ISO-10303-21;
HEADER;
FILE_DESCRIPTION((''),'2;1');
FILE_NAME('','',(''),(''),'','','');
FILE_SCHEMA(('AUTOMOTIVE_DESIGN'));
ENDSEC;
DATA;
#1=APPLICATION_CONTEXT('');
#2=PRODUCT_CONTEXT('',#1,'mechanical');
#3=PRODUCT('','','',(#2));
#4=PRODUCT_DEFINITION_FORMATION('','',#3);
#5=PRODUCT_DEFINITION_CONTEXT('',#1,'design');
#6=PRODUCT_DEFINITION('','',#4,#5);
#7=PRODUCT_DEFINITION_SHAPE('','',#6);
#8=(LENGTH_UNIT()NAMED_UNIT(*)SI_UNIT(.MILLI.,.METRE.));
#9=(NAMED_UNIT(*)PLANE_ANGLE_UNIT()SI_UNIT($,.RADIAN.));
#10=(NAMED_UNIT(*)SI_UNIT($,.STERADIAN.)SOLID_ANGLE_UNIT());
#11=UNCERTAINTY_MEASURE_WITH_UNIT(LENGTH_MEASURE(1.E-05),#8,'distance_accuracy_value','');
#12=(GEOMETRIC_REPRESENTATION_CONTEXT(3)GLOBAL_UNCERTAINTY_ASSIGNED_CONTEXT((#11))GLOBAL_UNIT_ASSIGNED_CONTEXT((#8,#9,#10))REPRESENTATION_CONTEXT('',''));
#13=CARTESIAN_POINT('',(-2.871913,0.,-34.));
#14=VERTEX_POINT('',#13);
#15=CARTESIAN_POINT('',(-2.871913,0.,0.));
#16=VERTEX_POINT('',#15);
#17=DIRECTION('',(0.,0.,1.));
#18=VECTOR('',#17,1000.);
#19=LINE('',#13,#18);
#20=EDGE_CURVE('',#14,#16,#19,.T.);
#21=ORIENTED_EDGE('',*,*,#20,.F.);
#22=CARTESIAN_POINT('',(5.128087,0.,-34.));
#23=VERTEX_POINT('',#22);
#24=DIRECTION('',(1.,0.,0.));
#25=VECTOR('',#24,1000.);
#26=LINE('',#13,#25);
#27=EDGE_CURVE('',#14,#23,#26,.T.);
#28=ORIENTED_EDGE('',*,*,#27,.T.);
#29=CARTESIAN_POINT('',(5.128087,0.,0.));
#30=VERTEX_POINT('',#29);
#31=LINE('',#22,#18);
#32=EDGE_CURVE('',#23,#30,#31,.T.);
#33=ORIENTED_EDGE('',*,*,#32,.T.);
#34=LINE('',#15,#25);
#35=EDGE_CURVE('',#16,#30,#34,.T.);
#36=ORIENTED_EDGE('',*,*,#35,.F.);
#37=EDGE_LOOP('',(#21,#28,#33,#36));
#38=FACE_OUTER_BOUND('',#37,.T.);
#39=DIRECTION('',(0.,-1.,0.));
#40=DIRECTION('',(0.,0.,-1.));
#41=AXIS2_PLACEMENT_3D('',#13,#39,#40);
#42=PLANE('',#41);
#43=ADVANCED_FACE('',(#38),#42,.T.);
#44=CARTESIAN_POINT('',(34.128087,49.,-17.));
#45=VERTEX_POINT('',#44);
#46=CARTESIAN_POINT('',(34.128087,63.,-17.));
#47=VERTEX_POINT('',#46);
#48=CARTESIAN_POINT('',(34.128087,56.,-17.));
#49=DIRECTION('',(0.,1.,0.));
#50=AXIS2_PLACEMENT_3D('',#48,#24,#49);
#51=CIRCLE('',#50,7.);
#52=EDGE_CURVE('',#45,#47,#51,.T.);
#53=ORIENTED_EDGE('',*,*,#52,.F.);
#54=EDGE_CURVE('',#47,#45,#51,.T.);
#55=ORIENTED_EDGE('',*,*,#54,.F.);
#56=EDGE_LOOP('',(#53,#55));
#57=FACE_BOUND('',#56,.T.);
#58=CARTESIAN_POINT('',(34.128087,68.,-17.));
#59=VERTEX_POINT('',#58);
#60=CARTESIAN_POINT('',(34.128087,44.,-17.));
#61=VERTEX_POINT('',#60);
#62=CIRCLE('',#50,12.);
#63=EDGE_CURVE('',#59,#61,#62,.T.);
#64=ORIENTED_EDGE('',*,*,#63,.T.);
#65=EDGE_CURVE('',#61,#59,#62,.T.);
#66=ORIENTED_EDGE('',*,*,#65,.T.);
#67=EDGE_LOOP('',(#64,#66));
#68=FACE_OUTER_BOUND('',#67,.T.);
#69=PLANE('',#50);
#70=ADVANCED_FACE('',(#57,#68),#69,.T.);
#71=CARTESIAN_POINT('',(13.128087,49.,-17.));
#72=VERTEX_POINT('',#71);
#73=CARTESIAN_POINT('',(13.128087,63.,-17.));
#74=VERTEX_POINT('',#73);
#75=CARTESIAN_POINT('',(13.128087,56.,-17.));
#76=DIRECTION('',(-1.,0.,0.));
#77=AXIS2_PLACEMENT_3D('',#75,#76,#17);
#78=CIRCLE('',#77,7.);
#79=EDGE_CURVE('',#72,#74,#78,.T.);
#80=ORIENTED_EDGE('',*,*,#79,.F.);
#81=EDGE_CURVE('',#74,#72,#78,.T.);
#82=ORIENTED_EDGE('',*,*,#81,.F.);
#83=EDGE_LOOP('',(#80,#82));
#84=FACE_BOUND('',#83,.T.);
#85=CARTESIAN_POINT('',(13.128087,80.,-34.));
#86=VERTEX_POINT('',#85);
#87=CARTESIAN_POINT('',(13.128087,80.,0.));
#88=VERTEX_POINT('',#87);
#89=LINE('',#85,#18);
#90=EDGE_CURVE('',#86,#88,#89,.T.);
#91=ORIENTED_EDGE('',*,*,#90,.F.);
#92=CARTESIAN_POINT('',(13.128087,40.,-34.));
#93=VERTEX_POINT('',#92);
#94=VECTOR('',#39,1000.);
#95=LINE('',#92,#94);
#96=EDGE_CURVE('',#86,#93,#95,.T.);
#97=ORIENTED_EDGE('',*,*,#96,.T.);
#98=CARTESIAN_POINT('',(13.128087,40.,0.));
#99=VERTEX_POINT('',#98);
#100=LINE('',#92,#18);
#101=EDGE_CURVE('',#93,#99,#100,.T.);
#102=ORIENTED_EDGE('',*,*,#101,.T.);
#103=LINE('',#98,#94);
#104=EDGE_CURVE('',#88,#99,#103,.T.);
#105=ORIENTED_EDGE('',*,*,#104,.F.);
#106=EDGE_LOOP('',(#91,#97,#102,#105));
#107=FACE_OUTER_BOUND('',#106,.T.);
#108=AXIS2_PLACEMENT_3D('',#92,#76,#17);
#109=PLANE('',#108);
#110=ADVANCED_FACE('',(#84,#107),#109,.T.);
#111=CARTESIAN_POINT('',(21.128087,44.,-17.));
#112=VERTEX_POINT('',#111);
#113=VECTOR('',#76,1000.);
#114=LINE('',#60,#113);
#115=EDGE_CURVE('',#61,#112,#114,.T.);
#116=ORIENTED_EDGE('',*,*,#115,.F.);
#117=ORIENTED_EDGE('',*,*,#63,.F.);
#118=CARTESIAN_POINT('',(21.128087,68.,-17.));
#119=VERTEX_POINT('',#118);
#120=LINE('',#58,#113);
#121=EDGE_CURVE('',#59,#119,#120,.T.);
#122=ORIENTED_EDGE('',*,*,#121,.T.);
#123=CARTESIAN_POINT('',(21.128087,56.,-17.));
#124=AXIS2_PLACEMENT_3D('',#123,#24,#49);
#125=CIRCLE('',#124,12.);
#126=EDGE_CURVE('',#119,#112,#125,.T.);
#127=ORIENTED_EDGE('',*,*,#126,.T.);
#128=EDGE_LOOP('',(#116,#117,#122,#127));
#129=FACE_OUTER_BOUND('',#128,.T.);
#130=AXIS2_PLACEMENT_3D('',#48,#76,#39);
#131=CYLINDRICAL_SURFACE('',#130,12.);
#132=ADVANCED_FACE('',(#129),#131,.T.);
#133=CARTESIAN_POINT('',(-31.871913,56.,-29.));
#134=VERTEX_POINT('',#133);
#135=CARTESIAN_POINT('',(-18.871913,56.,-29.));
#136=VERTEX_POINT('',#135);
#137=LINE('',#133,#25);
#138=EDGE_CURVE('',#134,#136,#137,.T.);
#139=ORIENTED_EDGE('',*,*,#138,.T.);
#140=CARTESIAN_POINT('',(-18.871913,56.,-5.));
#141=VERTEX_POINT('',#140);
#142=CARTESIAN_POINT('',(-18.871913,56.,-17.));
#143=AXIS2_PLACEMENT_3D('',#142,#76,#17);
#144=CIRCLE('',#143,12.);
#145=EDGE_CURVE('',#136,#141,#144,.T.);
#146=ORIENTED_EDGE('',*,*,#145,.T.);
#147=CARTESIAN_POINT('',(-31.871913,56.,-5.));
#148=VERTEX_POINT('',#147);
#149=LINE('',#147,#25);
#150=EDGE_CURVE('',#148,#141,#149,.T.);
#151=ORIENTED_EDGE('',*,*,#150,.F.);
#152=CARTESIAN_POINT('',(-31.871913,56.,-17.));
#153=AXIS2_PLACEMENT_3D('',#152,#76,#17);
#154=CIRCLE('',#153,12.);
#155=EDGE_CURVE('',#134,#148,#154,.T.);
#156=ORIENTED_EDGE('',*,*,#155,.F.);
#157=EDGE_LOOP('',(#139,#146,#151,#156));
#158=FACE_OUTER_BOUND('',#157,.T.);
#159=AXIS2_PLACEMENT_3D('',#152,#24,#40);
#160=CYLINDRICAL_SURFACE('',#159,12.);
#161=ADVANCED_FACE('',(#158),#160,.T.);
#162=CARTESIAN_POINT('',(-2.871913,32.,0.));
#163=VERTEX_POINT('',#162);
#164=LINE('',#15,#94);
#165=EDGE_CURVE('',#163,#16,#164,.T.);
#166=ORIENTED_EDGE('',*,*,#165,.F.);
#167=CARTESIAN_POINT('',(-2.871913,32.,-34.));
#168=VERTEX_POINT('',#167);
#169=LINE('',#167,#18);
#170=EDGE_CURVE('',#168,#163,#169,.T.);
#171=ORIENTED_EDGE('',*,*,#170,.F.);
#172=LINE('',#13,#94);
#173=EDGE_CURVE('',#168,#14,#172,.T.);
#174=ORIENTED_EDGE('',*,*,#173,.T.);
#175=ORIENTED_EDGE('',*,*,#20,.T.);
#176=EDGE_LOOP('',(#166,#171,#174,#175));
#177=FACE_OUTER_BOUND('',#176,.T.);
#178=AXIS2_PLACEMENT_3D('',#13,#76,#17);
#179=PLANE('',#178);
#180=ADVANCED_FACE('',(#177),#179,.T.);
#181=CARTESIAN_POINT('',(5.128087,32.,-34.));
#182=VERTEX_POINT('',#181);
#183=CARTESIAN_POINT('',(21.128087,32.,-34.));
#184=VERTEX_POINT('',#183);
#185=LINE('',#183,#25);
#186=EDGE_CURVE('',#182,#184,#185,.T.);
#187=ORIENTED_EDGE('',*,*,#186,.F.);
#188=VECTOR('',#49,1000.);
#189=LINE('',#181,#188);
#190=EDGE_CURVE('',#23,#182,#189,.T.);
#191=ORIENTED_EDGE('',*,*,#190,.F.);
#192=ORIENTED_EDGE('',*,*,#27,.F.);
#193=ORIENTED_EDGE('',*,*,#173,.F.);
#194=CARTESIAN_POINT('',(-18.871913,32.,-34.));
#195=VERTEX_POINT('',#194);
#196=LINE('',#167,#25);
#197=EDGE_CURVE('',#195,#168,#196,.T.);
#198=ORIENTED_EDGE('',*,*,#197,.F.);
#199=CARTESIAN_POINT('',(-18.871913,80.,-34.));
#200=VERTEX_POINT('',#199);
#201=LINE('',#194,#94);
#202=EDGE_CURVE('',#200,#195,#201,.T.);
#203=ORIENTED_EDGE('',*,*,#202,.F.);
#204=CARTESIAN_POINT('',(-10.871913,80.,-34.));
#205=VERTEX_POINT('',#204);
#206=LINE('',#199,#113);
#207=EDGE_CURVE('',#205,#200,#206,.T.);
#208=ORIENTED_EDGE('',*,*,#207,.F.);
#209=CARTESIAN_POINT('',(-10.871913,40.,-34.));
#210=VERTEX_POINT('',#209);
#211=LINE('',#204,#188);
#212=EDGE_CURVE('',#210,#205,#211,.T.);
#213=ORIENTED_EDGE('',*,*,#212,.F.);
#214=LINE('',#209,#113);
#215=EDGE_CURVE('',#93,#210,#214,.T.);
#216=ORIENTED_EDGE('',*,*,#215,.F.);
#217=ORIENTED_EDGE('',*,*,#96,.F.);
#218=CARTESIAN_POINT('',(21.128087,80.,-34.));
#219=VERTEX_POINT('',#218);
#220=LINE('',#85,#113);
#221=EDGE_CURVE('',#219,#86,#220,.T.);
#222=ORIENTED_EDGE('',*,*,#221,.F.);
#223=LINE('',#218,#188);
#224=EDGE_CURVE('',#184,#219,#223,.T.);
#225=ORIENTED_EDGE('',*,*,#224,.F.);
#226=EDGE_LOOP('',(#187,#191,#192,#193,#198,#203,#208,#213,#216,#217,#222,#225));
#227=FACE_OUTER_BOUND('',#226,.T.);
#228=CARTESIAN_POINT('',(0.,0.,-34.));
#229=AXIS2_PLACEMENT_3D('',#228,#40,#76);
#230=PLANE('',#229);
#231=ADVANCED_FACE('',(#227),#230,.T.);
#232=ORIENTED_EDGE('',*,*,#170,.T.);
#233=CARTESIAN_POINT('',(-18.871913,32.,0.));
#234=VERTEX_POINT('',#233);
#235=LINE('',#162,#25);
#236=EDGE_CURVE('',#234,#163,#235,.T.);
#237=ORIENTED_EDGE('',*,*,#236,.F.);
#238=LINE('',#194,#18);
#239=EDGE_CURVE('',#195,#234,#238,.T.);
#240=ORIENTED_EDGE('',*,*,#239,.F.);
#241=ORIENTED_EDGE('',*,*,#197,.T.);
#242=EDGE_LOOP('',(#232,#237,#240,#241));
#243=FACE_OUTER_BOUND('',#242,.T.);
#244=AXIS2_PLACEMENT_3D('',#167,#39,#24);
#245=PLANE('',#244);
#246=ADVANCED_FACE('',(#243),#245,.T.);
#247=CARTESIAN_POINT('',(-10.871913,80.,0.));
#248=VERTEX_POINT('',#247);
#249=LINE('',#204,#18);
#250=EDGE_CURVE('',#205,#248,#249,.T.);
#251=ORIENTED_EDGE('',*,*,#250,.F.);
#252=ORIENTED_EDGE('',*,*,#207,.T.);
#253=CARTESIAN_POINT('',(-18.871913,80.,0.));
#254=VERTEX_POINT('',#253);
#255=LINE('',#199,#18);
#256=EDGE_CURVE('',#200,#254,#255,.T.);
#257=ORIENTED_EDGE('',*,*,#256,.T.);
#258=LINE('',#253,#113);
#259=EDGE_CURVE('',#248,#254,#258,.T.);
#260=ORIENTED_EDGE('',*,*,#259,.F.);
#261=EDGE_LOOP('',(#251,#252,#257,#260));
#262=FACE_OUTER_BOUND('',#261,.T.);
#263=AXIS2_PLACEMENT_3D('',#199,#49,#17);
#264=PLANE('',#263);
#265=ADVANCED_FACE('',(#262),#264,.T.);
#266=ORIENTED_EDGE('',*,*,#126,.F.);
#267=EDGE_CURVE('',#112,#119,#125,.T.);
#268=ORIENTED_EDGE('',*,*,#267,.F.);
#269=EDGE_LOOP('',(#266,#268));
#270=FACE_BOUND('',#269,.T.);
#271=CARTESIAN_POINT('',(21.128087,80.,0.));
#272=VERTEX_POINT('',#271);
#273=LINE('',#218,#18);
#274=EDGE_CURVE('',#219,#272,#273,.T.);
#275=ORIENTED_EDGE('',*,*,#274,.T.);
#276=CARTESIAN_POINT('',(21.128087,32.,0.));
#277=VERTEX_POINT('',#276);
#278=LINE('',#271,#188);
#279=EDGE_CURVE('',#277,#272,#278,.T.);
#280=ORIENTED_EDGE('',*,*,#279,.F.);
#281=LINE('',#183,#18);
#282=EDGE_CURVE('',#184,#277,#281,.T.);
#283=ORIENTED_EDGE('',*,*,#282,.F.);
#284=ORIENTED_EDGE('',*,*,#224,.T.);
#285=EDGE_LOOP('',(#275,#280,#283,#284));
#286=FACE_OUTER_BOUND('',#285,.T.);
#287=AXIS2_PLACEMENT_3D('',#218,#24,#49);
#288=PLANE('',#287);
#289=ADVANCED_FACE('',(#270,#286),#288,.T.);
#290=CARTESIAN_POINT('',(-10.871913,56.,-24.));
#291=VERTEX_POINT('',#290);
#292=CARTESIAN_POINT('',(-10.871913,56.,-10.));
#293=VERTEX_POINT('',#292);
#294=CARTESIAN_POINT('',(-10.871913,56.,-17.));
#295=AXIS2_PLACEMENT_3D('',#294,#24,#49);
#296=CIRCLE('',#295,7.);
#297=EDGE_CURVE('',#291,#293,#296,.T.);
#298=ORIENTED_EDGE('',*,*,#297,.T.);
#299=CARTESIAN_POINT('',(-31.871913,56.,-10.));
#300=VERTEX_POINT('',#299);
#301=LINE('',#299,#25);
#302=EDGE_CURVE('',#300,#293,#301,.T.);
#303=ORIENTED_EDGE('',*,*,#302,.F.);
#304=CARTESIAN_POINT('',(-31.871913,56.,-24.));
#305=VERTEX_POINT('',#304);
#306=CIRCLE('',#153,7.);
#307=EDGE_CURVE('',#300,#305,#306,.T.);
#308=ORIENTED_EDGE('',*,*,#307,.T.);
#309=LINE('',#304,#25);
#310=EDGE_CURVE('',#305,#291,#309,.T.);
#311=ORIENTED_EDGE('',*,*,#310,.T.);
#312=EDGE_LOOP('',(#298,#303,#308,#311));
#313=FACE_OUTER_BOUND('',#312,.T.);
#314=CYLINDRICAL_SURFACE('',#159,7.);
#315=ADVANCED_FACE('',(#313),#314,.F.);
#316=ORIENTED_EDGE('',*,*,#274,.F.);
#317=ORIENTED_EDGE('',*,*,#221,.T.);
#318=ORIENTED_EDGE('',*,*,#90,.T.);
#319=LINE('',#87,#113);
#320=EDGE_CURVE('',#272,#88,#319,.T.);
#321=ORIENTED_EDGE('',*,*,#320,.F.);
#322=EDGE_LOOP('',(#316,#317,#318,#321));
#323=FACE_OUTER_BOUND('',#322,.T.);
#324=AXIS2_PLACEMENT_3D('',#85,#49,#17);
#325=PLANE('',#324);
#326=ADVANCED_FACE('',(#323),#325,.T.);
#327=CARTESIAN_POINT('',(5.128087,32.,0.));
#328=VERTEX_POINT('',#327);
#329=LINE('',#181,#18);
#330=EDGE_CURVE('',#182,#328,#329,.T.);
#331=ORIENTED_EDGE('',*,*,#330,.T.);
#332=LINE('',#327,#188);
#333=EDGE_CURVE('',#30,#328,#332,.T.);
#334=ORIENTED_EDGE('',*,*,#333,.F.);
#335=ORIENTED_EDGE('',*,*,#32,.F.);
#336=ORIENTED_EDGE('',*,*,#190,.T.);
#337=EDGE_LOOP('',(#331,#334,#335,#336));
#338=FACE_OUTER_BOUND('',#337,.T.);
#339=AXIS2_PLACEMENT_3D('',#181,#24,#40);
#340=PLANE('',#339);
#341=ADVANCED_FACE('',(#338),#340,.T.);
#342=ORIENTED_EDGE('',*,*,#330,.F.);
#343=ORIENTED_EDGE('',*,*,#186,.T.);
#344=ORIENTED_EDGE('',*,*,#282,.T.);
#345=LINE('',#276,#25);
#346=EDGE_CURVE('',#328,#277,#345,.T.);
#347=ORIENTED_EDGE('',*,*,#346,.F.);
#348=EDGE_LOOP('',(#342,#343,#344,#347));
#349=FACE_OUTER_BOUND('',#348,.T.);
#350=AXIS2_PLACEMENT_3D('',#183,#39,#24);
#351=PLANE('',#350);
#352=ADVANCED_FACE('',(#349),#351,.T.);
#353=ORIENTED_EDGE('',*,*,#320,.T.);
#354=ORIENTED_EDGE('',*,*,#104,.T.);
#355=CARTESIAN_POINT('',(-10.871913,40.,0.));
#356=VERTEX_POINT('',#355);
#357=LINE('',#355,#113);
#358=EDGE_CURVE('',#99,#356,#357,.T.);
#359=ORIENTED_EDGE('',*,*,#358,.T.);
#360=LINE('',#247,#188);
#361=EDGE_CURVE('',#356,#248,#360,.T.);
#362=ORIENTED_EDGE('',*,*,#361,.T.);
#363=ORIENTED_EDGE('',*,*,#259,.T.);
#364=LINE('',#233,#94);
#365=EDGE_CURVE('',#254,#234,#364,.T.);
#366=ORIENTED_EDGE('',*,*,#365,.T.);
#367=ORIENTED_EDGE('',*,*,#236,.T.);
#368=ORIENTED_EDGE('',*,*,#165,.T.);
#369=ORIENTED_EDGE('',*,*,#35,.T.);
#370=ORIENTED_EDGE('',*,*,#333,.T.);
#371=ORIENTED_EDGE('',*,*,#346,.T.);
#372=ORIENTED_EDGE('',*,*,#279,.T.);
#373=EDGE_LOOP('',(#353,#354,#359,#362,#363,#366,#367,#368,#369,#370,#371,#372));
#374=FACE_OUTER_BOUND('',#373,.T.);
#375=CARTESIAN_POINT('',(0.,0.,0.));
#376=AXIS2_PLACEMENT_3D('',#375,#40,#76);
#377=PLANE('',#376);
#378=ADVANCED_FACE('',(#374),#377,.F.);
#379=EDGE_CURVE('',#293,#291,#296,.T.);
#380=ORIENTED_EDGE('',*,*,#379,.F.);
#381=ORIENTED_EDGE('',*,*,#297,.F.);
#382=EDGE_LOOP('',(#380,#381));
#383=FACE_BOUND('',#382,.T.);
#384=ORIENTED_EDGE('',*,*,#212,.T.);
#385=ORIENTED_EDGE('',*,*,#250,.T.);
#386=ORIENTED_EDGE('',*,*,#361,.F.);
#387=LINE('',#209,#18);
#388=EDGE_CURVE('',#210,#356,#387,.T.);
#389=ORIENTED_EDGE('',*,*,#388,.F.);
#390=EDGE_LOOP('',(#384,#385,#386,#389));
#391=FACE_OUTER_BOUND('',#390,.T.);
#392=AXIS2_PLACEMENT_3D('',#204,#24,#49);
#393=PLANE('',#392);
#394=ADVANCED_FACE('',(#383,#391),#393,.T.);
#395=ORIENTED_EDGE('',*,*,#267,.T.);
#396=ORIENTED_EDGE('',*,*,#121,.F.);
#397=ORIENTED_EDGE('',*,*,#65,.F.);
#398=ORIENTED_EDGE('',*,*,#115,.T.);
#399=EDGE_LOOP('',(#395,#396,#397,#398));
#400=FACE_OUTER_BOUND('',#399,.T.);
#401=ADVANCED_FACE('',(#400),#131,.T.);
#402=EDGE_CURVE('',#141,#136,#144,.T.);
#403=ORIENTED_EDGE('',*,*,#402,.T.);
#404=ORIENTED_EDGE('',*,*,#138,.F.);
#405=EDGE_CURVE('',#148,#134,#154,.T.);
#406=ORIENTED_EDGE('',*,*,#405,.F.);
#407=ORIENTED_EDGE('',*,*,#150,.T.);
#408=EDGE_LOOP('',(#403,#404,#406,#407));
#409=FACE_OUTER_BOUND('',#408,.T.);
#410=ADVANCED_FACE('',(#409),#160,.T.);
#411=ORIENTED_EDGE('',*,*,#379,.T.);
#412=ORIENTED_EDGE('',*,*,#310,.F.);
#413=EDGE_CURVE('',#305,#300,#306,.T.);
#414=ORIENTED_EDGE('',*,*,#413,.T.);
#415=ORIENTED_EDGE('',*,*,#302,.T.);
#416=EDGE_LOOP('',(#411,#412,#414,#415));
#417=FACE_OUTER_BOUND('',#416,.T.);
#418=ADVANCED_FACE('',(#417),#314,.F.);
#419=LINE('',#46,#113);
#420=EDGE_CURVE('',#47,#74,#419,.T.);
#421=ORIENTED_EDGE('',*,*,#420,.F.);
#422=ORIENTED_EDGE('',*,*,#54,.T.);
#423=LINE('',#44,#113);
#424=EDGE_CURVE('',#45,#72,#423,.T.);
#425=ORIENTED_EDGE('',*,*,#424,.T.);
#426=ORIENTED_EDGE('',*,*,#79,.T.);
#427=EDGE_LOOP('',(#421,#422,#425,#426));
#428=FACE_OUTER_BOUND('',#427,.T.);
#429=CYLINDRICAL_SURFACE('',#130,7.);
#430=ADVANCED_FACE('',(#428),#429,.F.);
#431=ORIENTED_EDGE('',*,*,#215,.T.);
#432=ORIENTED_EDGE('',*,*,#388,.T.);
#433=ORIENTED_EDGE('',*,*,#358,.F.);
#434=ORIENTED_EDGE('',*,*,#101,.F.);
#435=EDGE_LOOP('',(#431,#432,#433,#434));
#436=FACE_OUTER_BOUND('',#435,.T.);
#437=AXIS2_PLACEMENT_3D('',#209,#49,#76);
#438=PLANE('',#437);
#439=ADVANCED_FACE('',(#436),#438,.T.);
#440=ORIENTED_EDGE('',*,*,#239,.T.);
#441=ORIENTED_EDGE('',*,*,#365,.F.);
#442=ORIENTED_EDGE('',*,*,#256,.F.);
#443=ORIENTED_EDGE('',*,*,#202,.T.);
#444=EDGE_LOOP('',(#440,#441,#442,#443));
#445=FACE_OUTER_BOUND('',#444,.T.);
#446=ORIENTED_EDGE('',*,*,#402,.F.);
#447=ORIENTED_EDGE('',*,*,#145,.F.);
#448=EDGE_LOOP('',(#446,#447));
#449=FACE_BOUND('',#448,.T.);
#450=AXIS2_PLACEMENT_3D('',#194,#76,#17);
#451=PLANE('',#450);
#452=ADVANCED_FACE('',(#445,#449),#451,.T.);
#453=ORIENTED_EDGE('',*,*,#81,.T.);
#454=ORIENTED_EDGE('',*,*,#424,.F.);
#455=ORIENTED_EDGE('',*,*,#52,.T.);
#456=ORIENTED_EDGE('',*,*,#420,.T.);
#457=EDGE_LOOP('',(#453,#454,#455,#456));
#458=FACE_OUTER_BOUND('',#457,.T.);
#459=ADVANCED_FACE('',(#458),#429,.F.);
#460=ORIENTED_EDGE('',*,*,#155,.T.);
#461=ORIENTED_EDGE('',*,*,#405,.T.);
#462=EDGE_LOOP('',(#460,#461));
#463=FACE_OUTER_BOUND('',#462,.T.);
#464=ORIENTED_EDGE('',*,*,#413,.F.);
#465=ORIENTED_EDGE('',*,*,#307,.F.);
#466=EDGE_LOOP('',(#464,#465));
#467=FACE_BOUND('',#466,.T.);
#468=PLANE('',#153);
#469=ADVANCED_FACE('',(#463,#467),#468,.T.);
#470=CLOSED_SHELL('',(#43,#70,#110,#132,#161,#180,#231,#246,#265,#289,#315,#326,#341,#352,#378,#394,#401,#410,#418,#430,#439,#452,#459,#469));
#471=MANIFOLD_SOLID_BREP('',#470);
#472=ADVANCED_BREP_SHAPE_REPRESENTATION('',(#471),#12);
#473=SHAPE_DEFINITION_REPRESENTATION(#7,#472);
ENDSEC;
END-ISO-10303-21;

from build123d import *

# Parameters (mm, degrees)
FORK_BODY_DEPTH          = 34
SIDE_BOSS_A_SKETCH_R     = 12
SIDE_BOSS_A_SKETCH_R_2   = 7
SIDE_BOSS_A_24X_14_DEPTH = 13
SIDE_START               = 13
SIDE_BOSS_B_SKETCH_R     = 12
SIDE_BOSS_B_SKETCH_R_2   = 7
SIDE_BOSS_B_24X_14_DEPTH = 13
PIN_HOLE_SKETCH_R        = 7
PIN_HOLE_DEPTH           = 102.808644034


with BuildPart() as part:
    # Fork Profile Sketch → Fork Body (new body)
    with BuildSketch(Plane.XY):
        Polygon((-2.871912694, 0), (-2.871912694, 32), (-18.871912694, 32), (-18.871912694, 80), (-10.871912694, 80), (-10.871912694, 40), (13.128087306, 40), (13.128087306, 80), (21.128087306, 80), (21.128087306, 32), (5.128087306, 32), (5.128087306, 0), align=None)
    extrude(amount=-FORK_BODY_DEPTH)

    # Side Boss A Sketch → Side Boss A Ø24xØ14 (add)
    with BuildSketch(Plane(origin=(21.128087306, 0, 0), x_dir=(0, 0, -1), z_dir=(1, 0, 0))):
        with Locations(Location((17, 56, 0), (0, 0, 270))):
            Circle(SIDE_BOSS_A_SKETCH_R)
        with Locations(Location((17, 56, 0), (0, 0, 270))):
            Circle(SIDE_BOSS_A_SKETCH_R_2, mode=Mode.SUBTRACT)
    extrude(amount=SIDE_BOSS_A_24X_14_DEPTH)

    # Side Boss B Sketch → Side Boss B Ø24xØ14 (add)
    with BuildSketch(Plane.ZY.offset(18.871912694).offset(SIDE_START)):
        with Locations(Location((-17, 56, 0), (0, 0, 270))):
            Circle(SIDE_BOSS_B_SKETCH_R)
        with Locations(Location((-17, 56, 0), (0, 0, 270))):
            Circle(SIDE_BOSS_B_SKETCH_R_2, mode=Mode.SUBTRACT)
    extrude(amount=-SIDE_BOSS_B_24X_14_DEPTH)

    # Pin Hole Sketch → Pin Hole (cut, through all)
    with BuildSketch(Plane.ZY.offset(18.871912694)):
        with Locations(Location((-17, 56, 0), (0, 0, 270))):
            Circle(PIN_HOLE_SKETCH_R)
    extrude(amount=-PIN_HOLE_DEPTH, mode=Mode.SUBTRACT)


solid = part.part
